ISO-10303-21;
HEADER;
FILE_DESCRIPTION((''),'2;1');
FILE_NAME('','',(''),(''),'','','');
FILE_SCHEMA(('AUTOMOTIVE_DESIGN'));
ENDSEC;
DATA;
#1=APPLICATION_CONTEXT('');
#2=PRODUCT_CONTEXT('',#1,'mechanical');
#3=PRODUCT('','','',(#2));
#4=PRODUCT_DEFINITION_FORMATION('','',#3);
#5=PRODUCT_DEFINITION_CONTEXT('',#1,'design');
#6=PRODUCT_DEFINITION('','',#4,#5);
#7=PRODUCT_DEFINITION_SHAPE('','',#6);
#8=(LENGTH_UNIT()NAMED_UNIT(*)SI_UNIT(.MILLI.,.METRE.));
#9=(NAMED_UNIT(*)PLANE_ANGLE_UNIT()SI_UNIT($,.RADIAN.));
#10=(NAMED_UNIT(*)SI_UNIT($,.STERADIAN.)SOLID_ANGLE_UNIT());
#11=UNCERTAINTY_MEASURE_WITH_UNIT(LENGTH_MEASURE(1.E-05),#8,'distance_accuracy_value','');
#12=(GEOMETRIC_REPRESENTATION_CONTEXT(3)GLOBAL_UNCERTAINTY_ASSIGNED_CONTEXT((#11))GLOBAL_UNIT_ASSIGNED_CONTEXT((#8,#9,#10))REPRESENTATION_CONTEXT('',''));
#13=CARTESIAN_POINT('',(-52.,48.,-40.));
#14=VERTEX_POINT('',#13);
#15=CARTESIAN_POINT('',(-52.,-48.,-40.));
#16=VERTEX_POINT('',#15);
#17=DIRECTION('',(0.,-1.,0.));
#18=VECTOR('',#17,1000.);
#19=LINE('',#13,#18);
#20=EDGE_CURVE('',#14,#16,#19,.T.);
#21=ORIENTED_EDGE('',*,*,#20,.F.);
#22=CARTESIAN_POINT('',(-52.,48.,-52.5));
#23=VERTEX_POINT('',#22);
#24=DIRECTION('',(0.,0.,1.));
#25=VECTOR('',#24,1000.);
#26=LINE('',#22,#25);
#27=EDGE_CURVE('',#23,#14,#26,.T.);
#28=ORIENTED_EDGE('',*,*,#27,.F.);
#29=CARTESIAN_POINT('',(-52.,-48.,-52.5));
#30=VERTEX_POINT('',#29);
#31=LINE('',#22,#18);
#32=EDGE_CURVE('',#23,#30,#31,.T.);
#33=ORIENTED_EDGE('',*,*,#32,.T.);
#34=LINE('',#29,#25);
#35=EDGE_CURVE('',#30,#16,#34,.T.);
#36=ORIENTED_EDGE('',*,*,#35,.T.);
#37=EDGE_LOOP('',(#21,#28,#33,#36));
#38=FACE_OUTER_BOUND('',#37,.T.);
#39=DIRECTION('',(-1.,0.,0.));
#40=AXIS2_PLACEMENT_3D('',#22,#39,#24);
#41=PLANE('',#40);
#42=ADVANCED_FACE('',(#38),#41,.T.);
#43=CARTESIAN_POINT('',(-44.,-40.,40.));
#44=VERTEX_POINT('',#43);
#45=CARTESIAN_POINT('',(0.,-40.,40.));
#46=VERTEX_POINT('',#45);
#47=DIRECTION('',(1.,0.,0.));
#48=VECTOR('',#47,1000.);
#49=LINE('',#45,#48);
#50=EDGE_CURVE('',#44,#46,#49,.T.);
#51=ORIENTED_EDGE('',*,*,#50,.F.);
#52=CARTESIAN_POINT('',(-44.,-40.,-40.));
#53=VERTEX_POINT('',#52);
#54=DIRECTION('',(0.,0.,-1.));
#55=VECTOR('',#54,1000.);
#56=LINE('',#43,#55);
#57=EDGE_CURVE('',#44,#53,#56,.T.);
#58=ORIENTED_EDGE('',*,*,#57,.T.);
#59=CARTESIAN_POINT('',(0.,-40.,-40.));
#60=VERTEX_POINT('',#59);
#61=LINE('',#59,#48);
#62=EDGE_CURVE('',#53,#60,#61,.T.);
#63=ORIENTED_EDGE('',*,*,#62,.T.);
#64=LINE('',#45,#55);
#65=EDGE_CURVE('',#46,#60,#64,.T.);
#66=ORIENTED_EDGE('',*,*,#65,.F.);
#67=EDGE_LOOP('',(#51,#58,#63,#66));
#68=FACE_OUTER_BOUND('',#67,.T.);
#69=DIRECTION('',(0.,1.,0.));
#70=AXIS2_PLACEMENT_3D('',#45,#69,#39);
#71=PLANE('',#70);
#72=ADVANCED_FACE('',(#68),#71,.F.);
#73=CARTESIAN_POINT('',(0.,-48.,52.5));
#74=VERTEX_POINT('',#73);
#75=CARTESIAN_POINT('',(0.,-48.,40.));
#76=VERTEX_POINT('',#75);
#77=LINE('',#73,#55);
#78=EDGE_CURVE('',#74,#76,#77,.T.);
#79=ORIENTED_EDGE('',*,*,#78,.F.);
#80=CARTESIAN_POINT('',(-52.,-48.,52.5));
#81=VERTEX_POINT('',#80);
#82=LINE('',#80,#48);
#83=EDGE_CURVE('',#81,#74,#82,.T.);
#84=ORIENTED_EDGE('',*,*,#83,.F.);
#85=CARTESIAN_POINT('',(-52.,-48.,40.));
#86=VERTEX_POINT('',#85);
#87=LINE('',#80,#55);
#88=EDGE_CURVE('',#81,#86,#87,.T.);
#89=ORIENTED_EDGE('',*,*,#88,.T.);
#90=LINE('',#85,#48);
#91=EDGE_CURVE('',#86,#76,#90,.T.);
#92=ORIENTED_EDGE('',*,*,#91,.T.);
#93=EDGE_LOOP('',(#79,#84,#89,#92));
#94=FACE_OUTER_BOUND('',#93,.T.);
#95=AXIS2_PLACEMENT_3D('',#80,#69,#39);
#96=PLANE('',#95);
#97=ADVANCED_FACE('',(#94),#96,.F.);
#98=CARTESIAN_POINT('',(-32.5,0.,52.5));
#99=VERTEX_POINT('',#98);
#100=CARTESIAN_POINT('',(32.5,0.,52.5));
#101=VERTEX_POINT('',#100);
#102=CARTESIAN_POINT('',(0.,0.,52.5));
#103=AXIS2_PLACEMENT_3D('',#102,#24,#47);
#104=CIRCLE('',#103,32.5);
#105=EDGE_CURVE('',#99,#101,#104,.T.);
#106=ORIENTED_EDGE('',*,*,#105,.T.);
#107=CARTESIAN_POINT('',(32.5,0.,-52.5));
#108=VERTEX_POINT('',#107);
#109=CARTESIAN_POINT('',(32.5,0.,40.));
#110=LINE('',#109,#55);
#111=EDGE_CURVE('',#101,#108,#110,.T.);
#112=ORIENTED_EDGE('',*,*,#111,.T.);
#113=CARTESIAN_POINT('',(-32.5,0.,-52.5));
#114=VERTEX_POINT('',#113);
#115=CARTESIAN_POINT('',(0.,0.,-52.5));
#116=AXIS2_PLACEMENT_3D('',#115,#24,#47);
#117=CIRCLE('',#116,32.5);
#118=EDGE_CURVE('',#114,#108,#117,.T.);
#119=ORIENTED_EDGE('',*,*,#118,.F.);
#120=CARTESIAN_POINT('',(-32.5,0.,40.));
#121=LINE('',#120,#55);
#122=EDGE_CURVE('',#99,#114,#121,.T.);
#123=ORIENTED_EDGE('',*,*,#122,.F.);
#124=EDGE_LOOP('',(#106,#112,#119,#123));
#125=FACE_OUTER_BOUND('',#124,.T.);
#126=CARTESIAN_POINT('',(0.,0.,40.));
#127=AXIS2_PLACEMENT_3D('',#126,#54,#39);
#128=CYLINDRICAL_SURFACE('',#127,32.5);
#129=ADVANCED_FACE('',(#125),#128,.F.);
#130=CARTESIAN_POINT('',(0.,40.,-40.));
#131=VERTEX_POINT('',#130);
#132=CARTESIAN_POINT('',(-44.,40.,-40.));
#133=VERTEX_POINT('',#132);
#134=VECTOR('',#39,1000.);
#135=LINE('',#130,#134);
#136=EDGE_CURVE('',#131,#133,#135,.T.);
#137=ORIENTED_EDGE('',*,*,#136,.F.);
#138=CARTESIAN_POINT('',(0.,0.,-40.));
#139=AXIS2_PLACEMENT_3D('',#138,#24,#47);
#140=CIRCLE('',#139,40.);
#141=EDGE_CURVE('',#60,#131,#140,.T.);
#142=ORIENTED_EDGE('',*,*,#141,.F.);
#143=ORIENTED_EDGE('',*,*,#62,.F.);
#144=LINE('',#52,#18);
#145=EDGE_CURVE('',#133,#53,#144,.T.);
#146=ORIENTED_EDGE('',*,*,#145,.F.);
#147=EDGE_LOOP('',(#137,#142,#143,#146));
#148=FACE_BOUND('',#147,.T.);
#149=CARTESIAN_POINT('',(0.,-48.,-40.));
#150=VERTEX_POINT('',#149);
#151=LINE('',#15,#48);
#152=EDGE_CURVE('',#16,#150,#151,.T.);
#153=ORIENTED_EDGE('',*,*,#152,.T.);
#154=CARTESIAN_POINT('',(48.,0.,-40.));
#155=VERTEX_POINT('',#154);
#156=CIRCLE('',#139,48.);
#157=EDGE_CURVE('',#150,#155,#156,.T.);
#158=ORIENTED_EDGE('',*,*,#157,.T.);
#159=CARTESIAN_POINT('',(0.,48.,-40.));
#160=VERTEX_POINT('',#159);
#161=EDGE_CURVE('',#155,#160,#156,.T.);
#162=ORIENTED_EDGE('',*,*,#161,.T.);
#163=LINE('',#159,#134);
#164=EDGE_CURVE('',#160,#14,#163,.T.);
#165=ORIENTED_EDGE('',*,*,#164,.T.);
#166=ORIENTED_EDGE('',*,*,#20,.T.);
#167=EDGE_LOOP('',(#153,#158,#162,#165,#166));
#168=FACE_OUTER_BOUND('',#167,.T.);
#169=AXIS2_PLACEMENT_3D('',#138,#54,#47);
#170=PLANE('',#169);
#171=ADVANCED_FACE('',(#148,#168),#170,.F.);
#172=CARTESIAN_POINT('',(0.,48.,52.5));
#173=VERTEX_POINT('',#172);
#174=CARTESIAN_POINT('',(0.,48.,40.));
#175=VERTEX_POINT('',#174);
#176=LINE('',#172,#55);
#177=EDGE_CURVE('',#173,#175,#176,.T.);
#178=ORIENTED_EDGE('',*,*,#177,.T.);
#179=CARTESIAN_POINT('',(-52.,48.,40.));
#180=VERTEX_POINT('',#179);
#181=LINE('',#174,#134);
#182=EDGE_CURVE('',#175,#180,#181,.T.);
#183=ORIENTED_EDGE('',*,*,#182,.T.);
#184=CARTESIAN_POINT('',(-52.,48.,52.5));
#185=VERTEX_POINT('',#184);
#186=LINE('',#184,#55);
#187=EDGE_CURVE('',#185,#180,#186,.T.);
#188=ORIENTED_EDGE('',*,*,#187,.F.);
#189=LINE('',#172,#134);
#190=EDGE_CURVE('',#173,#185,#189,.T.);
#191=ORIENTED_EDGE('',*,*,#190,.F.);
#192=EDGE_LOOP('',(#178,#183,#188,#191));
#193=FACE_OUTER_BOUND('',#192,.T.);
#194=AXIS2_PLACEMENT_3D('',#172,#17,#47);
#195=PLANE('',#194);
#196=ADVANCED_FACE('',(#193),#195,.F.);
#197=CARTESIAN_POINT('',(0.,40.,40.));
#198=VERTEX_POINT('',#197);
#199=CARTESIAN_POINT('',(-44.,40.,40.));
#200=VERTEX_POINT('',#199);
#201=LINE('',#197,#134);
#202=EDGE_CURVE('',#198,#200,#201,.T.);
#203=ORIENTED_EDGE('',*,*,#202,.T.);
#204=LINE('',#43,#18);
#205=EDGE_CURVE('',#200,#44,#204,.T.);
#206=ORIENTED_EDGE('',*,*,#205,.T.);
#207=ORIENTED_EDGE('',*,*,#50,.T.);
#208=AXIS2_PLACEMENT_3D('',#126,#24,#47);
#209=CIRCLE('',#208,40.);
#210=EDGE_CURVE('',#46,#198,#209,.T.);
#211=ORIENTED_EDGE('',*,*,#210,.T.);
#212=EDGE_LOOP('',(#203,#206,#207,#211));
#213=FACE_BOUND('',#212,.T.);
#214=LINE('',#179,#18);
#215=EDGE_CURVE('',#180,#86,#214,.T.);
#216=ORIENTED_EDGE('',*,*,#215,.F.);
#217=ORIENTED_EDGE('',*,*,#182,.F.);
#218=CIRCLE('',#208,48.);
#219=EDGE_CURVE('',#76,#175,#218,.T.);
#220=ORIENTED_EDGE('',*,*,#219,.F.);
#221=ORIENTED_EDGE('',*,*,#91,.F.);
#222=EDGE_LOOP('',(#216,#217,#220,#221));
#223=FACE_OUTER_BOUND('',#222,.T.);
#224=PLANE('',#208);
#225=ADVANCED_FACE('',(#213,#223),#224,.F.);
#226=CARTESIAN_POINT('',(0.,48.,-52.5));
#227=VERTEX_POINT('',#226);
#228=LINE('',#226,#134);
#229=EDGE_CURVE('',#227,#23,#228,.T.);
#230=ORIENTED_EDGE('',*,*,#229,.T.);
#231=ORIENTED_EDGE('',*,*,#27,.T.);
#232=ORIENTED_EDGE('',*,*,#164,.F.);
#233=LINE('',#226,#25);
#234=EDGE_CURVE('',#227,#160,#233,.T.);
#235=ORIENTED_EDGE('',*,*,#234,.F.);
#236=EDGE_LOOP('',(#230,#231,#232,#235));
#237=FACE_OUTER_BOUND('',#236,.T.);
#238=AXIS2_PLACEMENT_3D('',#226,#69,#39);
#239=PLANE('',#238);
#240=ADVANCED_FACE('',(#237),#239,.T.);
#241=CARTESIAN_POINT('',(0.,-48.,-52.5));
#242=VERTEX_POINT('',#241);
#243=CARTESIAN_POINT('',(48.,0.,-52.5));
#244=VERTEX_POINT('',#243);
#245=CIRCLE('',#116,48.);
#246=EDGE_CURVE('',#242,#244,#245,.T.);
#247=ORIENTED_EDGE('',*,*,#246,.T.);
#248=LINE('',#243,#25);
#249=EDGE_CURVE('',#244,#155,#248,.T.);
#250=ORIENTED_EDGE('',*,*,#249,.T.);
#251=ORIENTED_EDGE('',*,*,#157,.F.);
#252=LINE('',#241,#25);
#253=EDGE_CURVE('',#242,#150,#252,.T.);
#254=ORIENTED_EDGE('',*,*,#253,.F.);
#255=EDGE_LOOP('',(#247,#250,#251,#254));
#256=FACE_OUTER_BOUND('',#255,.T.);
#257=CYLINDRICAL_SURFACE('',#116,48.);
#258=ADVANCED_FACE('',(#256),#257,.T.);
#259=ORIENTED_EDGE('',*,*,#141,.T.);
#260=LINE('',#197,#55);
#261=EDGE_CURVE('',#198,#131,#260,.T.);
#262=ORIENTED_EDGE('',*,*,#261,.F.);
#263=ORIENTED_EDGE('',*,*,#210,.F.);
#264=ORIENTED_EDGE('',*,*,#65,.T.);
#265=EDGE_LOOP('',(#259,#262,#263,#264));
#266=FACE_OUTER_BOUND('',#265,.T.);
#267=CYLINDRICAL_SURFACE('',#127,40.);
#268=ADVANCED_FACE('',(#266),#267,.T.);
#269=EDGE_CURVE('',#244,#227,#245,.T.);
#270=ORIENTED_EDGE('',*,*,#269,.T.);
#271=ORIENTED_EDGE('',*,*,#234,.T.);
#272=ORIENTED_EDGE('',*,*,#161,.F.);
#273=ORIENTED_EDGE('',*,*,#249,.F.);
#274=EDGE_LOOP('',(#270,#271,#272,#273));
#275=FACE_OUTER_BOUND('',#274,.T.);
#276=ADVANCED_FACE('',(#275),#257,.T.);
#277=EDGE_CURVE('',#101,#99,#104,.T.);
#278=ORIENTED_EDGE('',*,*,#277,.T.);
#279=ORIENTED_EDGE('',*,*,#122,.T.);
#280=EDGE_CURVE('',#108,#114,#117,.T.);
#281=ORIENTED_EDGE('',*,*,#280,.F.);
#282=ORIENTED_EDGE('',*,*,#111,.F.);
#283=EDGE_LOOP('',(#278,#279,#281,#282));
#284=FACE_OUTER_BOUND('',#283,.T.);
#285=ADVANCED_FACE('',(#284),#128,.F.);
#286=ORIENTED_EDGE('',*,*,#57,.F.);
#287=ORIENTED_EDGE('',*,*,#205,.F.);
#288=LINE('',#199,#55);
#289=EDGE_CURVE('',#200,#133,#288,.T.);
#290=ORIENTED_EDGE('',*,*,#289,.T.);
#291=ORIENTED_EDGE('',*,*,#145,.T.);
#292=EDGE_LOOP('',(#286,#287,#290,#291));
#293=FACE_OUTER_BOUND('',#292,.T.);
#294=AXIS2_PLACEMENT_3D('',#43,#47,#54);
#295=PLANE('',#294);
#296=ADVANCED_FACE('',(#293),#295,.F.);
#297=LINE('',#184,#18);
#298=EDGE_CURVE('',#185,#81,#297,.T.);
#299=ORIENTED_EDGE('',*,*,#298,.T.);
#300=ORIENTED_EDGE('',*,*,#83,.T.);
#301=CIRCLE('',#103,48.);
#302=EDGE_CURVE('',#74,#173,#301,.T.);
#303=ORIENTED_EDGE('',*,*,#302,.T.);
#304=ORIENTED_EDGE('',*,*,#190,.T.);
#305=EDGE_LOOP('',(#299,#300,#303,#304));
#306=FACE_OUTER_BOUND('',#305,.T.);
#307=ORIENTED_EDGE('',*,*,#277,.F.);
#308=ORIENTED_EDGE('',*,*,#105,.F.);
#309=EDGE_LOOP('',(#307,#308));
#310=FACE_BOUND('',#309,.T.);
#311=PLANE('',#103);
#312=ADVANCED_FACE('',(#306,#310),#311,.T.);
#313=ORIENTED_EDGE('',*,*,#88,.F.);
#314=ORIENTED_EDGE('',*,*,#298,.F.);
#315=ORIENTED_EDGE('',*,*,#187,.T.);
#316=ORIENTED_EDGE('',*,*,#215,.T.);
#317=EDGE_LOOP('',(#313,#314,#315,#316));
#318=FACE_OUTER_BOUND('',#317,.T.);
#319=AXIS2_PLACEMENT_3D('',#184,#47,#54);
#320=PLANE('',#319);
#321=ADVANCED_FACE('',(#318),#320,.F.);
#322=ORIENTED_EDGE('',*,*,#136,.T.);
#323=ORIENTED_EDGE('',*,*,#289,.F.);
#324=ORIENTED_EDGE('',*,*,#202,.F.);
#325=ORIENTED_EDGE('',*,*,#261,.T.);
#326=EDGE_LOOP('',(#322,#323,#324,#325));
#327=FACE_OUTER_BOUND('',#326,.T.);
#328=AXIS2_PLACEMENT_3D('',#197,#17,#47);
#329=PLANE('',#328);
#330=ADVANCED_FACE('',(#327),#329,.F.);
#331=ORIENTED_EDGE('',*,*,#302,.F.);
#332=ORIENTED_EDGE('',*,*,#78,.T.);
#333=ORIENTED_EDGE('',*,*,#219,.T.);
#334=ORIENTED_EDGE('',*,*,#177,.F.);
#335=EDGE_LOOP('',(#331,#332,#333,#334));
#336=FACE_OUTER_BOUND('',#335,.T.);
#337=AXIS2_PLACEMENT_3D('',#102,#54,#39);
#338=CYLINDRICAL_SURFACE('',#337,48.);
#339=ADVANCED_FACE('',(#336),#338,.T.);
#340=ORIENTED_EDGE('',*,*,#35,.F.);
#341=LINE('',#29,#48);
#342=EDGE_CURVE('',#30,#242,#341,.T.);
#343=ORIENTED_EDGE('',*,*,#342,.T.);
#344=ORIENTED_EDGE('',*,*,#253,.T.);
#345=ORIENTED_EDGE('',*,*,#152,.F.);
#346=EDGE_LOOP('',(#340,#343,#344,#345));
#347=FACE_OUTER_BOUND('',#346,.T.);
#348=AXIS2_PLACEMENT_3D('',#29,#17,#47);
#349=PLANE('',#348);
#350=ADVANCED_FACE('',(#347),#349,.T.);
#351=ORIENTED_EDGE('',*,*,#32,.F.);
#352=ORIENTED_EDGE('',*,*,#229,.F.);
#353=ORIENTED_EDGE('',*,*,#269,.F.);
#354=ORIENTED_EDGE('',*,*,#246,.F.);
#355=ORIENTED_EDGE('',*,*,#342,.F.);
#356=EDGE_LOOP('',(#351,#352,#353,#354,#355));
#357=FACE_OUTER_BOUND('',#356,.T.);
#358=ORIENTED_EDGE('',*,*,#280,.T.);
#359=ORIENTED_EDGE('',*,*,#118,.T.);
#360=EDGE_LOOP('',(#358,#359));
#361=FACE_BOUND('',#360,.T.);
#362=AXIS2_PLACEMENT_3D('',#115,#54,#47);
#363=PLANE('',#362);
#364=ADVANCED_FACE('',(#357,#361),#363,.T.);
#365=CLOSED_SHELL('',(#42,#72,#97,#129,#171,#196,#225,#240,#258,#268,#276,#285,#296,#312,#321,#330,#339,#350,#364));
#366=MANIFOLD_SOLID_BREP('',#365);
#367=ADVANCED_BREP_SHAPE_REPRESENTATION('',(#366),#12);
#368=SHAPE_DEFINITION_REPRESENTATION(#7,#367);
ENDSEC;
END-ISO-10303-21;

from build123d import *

# Parameters (mm, degrees)
BUSH_PROFILE_SKETCH_R   = 32.5
BUSH_BODY_DEPTH         = 40
FLANGE_PROFILE_SKETCH_R = 32.5
END_FLANGE_DEPTH        = 12.5


with BuildPart() as part:
    # Bush Profile Sketch → Bush Body (new, symmetric)
    with BuildSketch(Plane.XY):
        with BuildLine():
            Line((0, 40), (-44, 40))
            Line((-44, 40), (-44, -40))
            Line((-44, -40), (0, -40))
            ThreePointArc((0, -40), (40, 0), (0, 40))
        make_face()
        Circle(BUSH_PROFILE_SKETCH_R, mode=Mode.SUBTRACT)
    extrude(amount=BUSH_BODY_DEPTH, both=True)

    # Flange Profile Sketch → End Flange (add)
    with BuildSketch(Plane.XY.offset(40)):
        with BuildLine():
            Line((0, 48), (-52, 48))
            Line((-52, 48), (-52, -48))
            Line((-52, -48), (0, -48))
            ThreePointArc((0, -48), (48, 0), (0, 48))
        make_face()
        Circle(FLANGE_PROFILE_SKETCH_R, mode=Mode.SUBTRACT)
    end_flange = extrude(amount=END_FLANGE_DEPTH)

    # End Flange Mirror: End Flange across plane
    add(end_flange.mirror(Plane.XY))


solid = part.part
